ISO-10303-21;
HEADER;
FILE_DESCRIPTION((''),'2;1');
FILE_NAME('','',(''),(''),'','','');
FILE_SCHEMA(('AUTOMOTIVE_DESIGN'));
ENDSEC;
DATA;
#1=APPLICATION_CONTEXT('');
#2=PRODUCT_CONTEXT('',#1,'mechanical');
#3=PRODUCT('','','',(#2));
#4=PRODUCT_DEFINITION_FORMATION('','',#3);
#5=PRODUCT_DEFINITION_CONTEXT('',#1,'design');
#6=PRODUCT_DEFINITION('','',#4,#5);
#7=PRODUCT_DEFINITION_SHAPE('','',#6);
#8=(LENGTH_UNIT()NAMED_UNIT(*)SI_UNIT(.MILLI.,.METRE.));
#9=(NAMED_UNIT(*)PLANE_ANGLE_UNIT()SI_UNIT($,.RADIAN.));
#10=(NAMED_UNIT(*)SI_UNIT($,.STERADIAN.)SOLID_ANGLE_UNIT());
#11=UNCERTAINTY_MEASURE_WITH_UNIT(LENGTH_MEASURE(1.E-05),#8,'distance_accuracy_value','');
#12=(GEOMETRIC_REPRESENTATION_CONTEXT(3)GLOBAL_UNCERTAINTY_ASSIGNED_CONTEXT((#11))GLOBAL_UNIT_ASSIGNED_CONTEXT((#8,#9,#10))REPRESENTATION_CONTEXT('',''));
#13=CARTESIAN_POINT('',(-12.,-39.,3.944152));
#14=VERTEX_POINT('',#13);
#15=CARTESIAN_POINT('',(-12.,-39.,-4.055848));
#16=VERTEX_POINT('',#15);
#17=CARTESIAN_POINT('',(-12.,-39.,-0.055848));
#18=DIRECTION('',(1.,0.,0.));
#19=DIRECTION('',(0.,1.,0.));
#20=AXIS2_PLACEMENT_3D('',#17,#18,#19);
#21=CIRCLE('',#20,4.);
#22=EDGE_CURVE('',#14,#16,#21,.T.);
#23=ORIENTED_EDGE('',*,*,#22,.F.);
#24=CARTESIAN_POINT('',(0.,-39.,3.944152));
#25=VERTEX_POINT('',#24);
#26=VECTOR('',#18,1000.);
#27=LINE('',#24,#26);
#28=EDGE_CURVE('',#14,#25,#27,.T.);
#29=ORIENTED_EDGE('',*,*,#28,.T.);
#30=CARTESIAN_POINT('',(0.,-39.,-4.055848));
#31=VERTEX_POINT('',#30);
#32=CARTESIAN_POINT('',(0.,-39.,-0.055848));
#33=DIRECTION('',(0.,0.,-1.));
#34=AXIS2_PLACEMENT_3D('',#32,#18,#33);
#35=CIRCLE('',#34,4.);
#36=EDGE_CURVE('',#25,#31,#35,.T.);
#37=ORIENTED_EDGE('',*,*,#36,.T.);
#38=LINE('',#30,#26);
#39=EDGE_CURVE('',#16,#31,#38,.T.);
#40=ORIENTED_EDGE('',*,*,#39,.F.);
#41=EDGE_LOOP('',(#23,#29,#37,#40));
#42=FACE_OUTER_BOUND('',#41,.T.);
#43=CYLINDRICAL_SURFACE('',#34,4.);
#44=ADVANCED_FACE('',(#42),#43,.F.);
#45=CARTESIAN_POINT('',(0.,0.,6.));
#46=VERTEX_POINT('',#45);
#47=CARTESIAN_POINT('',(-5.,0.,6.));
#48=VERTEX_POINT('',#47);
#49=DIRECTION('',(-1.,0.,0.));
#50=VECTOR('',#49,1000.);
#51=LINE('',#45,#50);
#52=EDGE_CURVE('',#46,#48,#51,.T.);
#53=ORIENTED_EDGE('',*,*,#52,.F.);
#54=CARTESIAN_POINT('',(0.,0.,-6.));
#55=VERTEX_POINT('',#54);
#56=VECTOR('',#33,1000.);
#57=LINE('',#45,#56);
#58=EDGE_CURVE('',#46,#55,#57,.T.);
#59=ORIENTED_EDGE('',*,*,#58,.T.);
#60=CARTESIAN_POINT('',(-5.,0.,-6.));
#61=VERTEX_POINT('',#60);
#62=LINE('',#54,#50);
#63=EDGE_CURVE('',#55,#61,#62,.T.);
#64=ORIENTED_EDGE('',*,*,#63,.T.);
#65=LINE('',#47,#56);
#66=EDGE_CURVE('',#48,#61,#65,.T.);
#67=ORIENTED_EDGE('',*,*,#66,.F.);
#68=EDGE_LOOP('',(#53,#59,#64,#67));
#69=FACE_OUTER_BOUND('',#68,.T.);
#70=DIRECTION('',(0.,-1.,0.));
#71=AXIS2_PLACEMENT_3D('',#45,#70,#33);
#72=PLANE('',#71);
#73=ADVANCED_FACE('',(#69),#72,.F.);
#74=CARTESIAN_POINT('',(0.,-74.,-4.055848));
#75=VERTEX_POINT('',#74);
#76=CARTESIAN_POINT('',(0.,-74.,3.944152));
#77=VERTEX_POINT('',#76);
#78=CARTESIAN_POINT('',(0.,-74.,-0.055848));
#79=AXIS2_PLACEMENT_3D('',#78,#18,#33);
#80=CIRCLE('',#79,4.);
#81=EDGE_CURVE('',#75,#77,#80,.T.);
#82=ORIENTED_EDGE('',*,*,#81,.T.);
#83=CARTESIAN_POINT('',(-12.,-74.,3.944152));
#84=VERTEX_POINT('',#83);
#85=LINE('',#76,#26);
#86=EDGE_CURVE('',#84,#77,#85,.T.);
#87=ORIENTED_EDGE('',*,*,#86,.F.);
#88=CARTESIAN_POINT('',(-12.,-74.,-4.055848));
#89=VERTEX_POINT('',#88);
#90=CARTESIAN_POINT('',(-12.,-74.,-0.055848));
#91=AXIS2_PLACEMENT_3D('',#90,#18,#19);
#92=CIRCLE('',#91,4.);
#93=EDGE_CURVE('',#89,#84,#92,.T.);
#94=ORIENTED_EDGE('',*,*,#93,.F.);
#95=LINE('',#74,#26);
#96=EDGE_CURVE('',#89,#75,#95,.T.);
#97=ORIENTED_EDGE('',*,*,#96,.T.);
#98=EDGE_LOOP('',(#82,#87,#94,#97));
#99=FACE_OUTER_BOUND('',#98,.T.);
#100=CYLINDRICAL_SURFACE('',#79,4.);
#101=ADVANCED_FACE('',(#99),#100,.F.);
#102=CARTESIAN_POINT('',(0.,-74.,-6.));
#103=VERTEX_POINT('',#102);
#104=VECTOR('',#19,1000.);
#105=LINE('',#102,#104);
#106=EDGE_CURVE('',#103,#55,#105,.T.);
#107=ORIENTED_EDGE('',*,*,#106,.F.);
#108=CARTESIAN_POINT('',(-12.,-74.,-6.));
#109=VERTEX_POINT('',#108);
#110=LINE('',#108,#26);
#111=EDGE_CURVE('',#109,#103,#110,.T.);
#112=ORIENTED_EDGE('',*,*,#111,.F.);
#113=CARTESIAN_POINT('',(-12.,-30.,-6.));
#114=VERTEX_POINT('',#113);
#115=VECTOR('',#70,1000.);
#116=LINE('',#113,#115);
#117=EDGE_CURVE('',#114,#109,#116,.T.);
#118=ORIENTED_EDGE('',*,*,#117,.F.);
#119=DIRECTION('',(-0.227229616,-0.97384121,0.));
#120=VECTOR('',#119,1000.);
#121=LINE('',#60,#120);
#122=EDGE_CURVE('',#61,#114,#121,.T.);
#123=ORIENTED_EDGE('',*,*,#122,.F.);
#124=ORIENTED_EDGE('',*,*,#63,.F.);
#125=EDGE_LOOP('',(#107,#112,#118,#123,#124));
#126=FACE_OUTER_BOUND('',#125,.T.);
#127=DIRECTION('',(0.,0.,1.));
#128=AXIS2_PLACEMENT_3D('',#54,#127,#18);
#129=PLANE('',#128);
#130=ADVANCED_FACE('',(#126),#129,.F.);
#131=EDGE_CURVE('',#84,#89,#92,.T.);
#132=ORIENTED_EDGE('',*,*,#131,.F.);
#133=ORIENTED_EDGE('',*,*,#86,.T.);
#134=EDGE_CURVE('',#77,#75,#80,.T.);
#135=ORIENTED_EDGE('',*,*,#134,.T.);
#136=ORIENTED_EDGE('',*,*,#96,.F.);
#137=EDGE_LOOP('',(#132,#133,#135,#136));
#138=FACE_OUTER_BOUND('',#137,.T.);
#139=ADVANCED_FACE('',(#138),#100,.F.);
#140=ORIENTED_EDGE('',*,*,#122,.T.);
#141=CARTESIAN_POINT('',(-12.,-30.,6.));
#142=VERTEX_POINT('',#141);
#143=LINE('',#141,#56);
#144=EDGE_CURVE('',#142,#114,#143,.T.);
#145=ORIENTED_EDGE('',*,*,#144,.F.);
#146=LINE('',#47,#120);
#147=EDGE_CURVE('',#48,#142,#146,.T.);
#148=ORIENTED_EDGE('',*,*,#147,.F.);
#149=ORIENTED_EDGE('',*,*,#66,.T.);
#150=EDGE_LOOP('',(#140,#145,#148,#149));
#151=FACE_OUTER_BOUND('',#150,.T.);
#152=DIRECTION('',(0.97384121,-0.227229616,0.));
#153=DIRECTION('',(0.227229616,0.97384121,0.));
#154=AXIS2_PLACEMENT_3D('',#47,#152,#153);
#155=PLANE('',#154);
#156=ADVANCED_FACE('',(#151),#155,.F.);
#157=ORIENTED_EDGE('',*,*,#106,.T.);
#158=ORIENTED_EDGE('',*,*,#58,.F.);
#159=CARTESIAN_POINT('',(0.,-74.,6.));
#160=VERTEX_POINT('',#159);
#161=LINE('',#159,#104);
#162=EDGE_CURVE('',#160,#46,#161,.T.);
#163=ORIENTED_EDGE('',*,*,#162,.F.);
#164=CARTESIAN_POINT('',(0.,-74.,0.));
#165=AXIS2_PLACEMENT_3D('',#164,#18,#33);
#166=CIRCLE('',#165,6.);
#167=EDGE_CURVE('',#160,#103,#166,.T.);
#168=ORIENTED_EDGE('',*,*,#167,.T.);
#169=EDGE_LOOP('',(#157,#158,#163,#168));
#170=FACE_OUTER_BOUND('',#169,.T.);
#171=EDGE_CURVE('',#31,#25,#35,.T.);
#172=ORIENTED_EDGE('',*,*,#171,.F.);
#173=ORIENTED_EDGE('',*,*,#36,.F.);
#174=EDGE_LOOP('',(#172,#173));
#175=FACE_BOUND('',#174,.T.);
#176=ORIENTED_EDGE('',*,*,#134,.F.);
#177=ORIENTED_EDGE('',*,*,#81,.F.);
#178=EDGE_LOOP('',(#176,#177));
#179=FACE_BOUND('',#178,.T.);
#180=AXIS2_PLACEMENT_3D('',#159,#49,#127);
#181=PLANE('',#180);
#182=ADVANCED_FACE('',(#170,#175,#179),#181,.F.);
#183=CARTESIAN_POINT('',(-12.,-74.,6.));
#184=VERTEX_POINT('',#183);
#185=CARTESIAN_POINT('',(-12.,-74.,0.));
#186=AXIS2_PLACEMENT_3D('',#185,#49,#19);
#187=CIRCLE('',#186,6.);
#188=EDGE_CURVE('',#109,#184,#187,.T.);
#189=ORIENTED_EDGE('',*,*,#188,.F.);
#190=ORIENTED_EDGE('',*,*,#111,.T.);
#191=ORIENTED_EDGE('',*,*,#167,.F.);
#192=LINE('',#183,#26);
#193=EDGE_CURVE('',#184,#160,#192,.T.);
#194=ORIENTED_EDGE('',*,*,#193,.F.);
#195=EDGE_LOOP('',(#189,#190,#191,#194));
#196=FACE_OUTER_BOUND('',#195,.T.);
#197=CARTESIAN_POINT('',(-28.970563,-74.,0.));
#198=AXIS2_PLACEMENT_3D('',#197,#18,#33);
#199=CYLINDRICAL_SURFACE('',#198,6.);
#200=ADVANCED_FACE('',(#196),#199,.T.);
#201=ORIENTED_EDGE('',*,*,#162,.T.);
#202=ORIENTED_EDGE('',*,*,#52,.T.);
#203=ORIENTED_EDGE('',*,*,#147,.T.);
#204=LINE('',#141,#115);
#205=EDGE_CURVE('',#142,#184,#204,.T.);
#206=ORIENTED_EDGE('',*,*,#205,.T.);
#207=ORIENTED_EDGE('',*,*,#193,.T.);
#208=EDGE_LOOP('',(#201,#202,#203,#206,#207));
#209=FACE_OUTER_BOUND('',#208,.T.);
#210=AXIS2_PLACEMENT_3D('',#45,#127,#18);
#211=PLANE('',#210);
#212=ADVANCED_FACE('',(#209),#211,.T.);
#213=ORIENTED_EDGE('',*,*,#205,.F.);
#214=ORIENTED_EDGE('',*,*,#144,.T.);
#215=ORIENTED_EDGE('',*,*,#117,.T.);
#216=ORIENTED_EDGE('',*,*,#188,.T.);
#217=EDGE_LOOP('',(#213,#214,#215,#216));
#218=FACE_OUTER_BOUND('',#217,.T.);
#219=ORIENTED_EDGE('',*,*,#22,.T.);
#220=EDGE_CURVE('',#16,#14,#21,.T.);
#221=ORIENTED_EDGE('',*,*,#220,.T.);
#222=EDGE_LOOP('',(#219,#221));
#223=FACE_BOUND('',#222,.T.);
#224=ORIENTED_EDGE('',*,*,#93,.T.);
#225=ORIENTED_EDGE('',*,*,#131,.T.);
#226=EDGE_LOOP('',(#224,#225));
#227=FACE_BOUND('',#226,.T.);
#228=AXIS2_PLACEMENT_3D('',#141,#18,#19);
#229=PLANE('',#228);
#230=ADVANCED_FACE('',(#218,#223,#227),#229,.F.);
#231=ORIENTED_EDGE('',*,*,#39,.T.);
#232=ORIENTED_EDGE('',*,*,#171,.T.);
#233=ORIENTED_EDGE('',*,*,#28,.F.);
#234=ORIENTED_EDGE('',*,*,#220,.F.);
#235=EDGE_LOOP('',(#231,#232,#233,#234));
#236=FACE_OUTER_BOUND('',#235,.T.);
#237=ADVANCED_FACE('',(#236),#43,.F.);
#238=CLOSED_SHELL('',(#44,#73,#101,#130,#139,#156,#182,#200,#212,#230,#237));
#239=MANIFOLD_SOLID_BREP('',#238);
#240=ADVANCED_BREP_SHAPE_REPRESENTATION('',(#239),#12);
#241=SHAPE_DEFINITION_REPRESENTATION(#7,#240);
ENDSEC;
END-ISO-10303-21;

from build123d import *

# Parameters (mm, degrees)
JAW_PLATE_12MM_DEPTH   = 6
ROUNDED_END_SKETCH_R   = 6
ROUNDED_END_BOSS_DEPTH = 12
TAPPED_HOLE_M8X1_25_D  = 8


with BuildPart() as part:
    # Jaw Profile Sketch → Jaw Plate 12mm (new, symmetric)
    with BuildSketch(Plane.XY):
        Polygon((0, 0), (-5, 0), (-12, -30), (-12, -74), (0, -74), align=None)
    extrude(amount=JAW_PLATE_12MM_DEPTH, both=True)

    # Rounded End Sketch → Rounded End Boss (add)
    with BuildSketch(Plane(origin=(0, 0, 0), x_dir=(0, 0, -1), z_dir=(1, 0, 0))):
        with Locations((0, -74)):
            Circle(ROUNDED_END_SKETCH_R)
    extrude(amount=-ROUNDED_END_BOSS_DEPTH)

    # Tapped Hole M8x1.25 (through all)
    with Locations(Plane(origin=(0, -74, -0.055848494), x_dir=(0, 0, 1), z_dir=(1, 0, 0))):
        with Locations((0, 0), (0, -35)):
            Hole(TAPPED_HOLE_M8X1_25_D / 2)


solid = part.part
